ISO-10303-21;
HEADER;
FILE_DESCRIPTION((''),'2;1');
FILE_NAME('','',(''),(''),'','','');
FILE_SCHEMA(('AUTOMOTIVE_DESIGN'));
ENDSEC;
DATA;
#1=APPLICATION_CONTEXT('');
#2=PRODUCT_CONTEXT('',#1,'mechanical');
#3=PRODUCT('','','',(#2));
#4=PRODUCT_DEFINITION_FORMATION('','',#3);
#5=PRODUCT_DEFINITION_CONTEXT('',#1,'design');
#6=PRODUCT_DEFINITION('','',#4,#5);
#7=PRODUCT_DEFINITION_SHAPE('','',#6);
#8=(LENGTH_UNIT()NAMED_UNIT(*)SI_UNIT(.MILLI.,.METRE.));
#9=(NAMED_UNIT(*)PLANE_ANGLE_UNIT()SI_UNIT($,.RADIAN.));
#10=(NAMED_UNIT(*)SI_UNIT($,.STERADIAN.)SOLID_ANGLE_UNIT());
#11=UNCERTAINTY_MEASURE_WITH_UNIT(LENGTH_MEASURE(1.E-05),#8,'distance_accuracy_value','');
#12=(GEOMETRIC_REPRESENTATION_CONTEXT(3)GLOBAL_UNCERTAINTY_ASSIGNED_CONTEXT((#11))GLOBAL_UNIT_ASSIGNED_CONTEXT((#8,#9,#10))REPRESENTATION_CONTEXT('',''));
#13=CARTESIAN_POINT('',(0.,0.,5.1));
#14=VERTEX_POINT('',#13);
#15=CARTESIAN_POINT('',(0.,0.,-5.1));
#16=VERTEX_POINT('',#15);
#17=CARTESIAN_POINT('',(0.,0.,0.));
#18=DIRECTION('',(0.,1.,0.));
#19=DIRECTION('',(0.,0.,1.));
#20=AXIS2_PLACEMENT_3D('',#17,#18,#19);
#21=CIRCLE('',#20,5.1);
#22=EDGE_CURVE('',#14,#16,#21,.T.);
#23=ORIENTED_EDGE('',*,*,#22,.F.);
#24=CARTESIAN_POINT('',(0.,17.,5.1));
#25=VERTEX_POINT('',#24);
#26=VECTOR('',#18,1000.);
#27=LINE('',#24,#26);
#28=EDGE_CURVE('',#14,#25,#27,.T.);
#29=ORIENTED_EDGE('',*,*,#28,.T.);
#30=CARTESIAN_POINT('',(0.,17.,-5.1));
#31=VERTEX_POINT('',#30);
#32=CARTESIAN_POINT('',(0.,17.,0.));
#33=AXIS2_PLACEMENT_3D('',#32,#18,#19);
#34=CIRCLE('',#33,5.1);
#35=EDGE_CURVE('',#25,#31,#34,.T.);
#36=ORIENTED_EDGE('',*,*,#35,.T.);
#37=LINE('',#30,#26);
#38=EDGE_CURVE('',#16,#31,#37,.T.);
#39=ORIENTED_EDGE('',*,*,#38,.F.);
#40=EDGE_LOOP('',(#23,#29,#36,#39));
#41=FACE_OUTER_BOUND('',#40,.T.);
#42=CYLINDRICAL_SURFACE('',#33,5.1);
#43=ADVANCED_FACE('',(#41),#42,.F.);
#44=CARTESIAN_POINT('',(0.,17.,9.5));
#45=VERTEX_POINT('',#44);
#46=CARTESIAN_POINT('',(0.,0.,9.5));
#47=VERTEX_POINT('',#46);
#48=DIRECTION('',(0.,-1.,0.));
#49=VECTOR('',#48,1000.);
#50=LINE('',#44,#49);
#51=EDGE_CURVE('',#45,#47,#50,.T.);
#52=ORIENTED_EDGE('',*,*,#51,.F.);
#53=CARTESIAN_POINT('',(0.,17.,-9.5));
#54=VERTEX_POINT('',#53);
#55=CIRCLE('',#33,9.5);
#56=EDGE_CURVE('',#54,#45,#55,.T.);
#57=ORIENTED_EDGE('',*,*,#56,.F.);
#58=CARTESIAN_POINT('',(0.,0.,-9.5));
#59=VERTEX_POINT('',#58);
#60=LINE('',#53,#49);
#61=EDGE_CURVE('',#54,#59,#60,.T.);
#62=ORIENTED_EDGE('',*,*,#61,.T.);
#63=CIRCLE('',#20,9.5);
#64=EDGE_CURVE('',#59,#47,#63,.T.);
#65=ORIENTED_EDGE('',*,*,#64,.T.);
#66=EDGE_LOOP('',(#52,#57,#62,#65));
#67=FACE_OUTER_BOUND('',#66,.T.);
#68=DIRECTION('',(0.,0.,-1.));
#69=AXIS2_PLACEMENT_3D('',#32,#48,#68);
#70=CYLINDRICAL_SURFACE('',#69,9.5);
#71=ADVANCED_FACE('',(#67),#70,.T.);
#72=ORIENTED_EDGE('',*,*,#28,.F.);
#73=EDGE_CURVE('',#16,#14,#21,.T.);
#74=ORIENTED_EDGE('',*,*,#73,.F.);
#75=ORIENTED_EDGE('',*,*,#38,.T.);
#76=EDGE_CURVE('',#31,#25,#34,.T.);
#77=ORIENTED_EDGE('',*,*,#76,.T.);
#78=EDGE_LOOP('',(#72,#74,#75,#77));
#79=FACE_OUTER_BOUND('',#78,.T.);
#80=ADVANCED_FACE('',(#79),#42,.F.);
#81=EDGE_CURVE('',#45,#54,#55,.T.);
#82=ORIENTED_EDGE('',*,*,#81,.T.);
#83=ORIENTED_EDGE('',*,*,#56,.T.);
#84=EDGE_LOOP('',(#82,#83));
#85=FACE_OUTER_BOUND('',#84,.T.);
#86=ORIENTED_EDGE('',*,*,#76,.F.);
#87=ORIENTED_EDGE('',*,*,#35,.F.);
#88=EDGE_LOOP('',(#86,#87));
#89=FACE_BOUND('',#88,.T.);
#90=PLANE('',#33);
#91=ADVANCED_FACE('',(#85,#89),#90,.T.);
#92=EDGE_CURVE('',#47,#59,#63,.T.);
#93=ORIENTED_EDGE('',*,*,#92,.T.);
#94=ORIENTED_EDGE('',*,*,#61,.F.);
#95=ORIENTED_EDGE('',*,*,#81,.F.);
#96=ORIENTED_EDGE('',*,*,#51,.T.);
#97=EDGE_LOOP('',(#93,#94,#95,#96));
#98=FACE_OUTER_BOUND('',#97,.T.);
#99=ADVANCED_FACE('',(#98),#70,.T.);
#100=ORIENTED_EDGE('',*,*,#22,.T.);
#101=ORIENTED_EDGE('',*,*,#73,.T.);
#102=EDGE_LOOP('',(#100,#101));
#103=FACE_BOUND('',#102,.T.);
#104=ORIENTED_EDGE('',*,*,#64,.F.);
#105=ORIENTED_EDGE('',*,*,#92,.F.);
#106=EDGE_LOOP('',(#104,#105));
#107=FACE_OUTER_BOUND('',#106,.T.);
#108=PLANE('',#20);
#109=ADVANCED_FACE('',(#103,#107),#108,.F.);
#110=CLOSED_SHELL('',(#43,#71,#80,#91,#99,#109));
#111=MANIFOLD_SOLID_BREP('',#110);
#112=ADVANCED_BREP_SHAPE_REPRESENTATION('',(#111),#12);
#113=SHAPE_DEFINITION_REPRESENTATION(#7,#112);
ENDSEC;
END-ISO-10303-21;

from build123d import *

# Parameters (mm, degrees)
SKETCH1_R              = 9.5
SKETCH1_R_2            = 4.5
BOSS_EXTRUDE1_DEPTH    = 17
M12_TAPPED_HOLE1_D     = 10.2
M12_TAPPED_HOLE1_DEPTH = 32.75
M12_TAPPED_HOLE1_TIP   = 3.064389157


with BuildPart() as part:
    # Sketch1 → Boss-Extrude1 (new body)
    with BuildSketch(Plane(origin=(0, 0, 0), x_dir=(1, 0, 0), z_dir=(0, 1, 0))):
        with Locations(Location((0, 0, 0), (0, 0, 270))):
            Circle(SKETCH1_R)
        with Locations(Location((0, 0, 0), (0, 0, 270))):
            Circle(SKETCH1_R_2, mode=Mode.SUBTRACT)
    extrude(amount=BOSS_EXTRUDE1_DEPTH)

    # M12 Tapped Hole1
    with Locations(Plane(origin=(0, 17, 0), x_dir=(1, 0, 0), z_dir=(0, 1, 0))):
        with Locations((0, 0)):
            Hole(M12_TAPPED_HOLE1_D / 2, depth=M12_TAPPED_HOLE1_DEPTH)
            with Locations((0, 0, -(M12_TAPPED_HOLE1_DEPTH + M12_TAPPED_HOLE1_TIP / 2))):  # 118° drill point
                Cone(0, M12_TAPPED_HOLE1_D / 2, M12_TAPPED_HOLE1_TIP, mode=Mode.SUBTRACT)


solid = part.part
